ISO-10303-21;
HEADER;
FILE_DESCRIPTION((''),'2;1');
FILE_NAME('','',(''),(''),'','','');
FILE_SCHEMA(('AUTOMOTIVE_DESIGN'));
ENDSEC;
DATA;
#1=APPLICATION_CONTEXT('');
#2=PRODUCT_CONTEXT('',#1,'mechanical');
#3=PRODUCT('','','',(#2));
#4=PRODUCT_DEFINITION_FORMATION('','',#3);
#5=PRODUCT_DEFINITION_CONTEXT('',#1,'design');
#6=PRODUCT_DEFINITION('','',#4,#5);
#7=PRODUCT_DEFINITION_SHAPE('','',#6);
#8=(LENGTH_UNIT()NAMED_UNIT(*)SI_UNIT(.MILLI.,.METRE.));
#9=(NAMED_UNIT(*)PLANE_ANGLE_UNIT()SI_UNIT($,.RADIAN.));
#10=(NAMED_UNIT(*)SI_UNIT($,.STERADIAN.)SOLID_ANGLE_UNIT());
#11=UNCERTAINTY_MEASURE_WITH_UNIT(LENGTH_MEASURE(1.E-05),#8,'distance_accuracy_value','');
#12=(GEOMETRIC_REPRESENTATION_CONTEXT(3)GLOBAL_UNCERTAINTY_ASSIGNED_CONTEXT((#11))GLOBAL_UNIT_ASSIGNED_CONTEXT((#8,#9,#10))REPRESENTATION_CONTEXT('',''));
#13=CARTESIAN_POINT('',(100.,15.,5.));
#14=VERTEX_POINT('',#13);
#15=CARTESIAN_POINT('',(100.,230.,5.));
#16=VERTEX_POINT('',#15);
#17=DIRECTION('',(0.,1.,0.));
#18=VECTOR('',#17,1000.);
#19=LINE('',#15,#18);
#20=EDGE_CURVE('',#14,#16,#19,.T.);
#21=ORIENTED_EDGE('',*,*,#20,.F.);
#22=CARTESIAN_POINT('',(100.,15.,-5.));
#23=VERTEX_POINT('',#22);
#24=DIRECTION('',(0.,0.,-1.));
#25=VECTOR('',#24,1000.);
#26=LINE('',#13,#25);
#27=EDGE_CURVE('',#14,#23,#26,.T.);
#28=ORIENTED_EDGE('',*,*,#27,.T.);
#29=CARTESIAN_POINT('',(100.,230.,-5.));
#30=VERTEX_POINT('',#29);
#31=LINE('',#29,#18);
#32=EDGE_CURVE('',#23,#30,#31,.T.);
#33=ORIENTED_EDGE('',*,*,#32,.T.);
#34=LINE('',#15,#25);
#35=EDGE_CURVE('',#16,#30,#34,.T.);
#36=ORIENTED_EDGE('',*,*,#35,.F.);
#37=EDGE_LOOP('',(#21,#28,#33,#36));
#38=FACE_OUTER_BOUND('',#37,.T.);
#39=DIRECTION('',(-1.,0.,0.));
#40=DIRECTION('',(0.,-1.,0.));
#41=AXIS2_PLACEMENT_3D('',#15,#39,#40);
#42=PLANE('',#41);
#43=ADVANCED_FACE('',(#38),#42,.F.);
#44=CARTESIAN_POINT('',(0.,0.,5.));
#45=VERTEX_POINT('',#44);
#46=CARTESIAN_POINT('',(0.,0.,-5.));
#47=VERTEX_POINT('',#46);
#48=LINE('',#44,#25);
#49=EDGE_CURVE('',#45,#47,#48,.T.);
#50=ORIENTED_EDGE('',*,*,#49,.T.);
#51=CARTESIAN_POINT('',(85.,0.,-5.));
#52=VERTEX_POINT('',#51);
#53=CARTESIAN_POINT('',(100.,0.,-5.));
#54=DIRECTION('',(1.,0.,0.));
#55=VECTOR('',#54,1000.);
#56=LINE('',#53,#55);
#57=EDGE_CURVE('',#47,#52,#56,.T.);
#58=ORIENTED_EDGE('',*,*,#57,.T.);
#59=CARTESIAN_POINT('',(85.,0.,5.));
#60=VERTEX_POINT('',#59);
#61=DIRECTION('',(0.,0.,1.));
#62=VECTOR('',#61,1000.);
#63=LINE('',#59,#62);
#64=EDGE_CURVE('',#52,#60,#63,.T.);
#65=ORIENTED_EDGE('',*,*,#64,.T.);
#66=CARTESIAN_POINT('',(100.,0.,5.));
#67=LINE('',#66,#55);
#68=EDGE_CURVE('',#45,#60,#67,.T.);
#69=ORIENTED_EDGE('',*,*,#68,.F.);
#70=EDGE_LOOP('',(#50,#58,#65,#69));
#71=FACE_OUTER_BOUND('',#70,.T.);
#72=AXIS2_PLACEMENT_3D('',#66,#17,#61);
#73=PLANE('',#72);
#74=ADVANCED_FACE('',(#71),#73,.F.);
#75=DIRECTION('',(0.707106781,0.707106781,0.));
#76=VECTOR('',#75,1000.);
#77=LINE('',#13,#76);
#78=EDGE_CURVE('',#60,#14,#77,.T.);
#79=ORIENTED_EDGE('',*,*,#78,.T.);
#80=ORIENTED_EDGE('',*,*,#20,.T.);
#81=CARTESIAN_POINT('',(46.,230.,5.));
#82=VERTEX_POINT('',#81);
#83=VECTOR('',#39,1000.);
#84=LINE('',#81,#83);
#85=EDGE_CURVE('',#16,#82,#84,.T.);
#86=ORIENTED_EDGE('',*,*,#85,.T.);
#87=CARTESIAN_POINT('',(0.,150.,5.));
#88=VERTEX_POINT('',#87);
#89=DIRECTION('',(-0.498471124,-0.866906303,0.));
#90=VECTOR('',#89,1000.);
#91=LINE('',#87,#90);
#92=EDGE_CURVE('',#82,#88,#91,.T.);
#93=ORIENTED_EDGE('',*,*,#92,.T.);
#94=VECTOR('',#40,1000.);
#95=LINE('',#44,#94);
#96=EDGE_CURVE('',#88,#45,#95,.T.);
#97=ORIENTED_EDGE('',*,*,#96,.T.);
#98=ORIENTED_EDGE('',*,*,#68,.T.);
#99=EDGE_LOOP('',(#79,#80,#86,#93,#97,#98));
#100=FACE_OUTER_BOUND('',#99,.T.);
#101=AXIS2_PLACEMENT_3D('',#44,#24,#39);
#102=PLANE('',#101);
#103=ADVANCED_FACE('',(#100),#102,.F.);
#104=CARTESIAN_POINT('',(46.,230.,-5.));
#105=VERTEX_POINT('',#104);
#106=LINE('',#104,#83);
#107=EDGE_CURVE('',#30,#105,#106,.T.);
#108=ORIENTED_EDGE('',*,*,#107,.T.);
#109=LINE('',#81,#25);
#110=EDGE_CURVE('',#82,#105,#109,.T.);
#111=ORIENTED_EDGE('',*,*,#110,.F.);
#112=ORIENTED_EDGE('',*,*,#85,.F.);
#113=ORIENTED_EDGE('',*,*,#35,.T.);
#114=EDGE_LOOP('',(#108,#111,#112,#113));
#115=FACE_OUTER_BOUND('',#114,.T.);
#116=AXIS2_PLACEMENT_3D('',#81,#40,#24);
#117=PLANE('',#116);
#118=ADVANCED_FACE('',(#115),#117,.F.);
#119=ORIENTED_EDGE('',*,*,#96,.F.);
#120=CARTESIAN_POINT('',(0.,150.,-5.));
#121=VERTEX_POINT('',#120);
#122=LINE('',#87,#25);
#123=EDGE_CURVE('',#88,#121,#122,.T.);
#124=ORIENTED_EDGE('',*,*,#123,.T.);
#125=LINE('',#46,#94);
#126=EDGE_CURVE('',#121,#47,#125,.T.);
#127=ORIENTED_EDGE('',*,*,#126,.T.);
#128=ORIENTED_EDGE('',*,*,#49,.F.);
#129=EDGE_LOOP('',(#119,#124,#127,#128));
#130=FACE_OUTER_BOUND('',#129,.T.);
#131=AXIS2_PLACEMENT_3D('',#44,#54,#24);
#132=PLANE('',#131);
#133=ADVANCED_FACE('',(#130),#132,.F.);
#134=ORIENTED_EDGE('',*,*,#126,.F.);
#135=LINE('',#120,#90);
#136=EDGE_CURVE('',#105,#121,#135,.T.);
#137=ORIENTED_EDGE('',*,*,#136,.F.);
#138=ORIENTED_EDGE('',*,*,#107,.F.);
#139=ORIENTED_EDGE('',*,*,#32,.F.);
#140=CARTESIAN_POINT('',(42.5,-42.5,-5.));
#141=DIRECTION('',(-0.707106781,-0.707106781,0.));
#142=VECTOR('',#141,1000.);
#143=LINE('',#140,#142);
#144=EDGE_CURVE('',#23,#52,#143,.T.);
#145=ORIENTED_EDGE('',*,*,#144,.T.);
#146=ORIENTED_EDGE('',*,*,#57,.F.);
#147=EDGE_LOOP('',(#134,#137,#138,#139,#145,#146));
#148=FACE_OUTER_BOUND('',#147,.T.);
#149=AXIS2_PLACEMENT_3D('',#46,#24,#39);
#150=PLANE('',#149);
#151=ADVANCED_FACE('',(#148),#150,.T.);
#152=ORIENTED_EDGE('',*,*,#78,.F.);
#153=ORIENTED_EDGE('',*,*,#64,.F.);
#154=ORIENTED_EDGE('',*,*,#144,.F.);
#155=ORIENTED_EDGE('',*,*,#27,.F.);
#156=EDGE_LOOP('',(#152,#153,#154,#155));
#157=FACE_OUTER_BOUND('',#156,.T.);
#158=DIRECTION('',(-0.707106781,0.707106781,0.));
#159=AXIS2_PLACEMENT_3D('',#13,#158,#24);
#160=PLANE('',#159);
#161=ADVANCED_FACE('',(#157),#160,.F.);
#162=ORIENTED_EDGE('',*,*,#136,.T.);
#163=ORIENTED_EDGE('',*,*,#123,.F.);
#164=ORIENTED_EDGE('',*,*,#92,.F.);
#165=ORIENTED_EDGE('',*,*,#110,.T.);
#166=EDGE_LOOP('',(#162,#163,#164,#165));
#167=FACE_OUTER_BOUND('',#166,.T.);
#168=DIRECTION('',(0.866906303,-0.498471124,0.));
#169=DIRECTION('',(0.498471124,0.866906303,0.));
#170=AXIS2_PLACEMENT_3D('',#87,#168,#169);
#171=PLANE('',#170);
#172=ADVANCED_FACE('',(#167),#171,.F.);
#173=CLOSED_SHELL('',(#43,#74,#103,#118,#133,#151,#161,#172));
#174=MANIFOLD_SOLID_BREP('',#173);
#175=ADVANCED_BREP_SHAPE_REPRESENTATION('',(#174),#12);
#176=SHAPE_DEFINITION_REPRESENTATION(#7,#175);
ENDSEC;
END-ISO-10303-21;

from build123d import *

# Parameters (mm, degrees)
EXTRUDE_1_DEPTH = 5
CHAMFER_1_SIZE  = 15


with BuildPart() as part:
    # 草图1 → 凸台-拉伸1 (new, symmetric)
    with BuildSketch(Plane.XY):
        Polygon((0, 0), (0, 150), (46, 230), (100, 230), (100, 0), align=None)
    extrude(amount=EXTRUDE_1_DEPTH, both=True)

    # 倒角1
    chamfer_1_edges = [part.edges().sort_by_distance(p)[0] for p in [
        (100, 0, 0),
    ]]
    chamfer(chamfer_1_edges, length=CHAMFER_1_SIZE)


solid = part.part
